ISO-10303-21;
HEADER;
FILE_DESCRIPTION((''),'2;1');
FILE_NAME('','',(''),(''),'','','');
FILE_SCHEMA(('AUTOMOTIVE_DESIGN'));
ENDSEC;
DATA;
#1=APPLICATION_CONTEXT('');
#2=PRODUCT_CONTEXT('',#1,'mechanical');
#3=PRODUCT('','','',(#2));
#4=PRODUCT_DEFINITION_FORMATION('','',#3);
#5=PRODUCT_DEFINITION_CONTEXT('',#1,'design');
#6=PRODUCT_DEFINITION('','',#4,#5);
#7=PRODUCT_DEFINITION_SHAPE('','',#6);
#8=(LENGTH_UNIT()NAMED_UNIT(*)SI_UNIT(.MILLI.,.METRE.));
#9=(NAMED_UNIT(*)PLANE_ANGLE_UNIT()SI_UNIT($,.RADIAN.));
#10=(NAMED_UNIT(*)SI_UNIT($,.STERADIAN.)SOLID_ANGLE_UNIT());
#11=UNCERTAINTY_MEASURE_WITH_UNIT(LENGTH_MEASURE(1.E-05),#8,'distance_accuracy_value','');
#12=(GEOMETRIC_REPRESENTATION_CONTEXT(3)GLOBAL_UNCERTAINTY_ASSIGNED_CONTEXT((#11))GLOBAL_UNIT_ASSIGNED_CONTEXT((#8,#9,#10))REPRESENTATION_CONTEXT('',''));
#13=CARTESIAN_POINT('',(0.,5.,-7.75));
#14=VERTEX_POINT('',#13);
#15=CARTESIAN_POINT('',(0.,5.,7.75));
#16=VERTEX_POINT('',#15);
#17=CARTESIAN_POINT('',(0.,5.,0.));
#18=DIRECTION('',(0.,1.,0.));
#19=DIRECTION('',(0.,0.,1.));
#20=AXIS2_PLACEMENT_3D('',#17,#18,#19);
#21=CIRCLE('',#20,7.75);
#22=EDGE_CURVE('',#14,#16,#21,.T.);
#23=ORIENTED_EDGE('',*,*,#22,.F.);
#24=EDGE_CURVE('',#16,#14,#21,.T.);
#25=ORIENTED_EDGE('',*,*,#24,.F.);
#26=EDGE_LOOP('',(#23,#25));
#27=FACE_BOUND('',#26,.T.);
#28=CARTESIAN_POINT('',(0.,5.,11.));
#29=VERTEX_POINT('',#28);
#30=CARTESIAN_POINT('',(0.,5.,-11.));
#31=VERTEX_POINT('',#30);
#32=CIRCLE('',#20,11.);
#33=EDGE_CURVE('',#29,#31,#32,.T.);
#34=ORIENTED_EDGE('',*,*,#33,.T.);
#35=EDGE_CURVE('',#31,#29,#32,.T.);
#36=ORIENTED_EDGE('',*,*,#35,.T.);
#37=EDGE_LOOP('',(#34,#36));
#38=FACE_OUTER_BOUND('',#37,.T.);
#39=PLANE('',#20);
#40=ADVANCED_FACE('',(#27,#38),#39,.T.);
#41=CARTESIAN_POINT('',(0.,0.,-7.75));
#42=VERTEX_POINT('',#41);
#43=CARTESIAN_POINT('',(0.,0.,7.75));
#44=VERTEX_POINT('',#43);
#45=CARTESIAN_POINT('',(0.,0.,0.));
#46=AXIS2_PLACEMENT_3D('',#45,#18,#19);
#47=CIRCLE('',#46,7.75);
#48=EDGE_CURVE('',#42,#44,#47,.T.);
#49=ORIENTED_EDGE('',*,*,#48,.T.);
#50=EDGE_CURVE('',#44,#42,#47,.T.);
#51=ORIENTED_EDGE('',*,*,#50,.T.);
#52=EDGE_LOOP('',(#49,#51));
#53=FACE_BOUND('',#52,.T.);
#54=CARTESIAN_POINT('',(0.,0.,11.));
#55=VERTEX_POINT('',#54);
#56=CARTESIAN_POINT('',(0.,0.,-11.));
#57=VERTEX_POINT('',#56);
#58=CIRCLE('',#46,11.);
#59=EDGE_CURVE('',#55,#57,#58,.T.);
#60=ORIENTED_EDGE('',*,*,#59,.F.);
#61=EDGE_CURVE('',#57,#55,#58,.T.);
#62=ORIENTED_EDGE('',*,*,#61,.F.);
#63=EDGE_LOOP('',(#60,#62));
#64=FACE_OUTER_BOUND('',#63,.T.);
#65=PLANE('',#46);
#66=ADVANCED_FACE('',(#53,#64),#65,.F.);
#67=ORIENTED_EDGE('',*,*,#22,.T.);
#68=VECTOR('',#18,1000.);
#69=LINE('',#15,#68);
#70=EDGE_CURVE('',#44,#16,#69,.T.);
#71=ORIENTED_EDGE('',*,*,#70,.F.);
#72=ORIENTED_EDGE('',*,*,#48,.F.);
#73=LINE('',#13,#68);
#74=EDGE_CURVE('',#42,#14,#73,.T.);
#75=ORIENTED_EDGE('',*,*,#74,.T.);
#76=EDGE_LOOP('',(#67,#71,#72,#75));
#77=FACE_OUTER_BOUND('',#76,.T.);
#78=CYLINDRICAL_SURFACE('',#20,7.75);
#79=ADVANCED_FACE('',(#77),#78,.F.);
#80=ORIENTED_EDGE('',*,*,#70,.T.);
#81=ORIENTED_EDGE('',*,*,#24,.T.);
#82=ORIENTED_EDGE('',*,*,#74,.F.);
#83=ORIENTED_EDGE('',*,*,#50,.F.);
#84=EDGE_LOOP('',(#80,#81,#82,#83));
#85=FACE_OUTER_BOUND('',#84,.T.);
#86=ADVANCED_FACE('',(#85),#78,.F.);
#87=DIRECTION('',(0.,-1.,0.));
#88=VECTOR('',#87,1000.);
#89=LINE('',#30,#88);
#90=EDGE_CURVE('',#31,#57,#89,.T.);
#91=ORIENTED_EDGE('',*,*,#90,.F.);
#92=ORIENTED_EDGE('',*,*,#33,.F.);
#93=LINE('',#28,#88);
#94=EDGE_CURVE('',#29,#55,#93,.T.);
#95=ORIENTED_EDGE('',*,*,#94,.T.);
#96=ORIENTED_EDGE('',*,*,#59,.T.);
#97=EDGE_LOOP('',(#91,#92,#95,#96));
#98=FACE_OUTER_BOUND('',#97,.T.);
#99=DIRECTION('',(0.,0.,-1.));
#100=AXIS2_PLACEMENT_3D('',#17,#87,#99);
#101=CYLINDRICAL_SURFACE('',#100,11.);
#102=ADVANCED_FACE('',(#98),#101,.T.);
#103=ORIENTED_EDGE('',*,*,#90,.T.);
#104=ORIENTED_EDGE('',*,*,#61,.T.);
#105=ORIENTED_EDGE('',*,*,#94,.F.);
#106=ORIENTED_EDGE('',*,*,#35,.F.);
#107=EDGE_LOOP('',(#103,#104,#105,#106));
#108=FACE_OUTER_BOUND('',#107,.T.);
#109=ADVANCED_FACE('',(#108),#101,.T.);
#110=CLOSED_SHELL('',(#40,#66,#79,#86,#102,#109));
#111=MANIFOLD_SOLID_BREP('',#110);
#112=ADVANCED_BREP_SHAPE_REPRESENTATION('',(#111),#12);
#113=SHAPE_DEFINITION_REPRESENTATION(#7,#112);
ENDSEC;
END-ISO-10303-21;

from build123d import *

# Parameters (mm, degrees)
SKETCH2_R           = 11
BOSS_EXTRUDE1_DEPTH = 5
M18_TAPPED_HOLE1_D  = 15.5


with BuildPart() as part:
    # Sketch2 → Boss-Extrude1 (new body)
    with BuildSketch(Plane(origin=(0, 0, 0), x_dir=(1, 0, 0), z_dir=(0, 1, 0))):
        with Locations(Location((0, 0, 0), (0, 0, 270))):
            Circle(SKETCH2_R)
    extrude(amount=BOSS_EXTRUDE1_DEPTH)

    # M18 Tapped Hole1 (through all)
    with Locations(Plane(origin=(0, 5, 0), x_dir=(1, 0, 0), z_dir=(0, 1, 0))):
        with Locations((0, 0)):
            Hole(M18_TAPPED_HOLE1_D / 2)


solid = part.part
